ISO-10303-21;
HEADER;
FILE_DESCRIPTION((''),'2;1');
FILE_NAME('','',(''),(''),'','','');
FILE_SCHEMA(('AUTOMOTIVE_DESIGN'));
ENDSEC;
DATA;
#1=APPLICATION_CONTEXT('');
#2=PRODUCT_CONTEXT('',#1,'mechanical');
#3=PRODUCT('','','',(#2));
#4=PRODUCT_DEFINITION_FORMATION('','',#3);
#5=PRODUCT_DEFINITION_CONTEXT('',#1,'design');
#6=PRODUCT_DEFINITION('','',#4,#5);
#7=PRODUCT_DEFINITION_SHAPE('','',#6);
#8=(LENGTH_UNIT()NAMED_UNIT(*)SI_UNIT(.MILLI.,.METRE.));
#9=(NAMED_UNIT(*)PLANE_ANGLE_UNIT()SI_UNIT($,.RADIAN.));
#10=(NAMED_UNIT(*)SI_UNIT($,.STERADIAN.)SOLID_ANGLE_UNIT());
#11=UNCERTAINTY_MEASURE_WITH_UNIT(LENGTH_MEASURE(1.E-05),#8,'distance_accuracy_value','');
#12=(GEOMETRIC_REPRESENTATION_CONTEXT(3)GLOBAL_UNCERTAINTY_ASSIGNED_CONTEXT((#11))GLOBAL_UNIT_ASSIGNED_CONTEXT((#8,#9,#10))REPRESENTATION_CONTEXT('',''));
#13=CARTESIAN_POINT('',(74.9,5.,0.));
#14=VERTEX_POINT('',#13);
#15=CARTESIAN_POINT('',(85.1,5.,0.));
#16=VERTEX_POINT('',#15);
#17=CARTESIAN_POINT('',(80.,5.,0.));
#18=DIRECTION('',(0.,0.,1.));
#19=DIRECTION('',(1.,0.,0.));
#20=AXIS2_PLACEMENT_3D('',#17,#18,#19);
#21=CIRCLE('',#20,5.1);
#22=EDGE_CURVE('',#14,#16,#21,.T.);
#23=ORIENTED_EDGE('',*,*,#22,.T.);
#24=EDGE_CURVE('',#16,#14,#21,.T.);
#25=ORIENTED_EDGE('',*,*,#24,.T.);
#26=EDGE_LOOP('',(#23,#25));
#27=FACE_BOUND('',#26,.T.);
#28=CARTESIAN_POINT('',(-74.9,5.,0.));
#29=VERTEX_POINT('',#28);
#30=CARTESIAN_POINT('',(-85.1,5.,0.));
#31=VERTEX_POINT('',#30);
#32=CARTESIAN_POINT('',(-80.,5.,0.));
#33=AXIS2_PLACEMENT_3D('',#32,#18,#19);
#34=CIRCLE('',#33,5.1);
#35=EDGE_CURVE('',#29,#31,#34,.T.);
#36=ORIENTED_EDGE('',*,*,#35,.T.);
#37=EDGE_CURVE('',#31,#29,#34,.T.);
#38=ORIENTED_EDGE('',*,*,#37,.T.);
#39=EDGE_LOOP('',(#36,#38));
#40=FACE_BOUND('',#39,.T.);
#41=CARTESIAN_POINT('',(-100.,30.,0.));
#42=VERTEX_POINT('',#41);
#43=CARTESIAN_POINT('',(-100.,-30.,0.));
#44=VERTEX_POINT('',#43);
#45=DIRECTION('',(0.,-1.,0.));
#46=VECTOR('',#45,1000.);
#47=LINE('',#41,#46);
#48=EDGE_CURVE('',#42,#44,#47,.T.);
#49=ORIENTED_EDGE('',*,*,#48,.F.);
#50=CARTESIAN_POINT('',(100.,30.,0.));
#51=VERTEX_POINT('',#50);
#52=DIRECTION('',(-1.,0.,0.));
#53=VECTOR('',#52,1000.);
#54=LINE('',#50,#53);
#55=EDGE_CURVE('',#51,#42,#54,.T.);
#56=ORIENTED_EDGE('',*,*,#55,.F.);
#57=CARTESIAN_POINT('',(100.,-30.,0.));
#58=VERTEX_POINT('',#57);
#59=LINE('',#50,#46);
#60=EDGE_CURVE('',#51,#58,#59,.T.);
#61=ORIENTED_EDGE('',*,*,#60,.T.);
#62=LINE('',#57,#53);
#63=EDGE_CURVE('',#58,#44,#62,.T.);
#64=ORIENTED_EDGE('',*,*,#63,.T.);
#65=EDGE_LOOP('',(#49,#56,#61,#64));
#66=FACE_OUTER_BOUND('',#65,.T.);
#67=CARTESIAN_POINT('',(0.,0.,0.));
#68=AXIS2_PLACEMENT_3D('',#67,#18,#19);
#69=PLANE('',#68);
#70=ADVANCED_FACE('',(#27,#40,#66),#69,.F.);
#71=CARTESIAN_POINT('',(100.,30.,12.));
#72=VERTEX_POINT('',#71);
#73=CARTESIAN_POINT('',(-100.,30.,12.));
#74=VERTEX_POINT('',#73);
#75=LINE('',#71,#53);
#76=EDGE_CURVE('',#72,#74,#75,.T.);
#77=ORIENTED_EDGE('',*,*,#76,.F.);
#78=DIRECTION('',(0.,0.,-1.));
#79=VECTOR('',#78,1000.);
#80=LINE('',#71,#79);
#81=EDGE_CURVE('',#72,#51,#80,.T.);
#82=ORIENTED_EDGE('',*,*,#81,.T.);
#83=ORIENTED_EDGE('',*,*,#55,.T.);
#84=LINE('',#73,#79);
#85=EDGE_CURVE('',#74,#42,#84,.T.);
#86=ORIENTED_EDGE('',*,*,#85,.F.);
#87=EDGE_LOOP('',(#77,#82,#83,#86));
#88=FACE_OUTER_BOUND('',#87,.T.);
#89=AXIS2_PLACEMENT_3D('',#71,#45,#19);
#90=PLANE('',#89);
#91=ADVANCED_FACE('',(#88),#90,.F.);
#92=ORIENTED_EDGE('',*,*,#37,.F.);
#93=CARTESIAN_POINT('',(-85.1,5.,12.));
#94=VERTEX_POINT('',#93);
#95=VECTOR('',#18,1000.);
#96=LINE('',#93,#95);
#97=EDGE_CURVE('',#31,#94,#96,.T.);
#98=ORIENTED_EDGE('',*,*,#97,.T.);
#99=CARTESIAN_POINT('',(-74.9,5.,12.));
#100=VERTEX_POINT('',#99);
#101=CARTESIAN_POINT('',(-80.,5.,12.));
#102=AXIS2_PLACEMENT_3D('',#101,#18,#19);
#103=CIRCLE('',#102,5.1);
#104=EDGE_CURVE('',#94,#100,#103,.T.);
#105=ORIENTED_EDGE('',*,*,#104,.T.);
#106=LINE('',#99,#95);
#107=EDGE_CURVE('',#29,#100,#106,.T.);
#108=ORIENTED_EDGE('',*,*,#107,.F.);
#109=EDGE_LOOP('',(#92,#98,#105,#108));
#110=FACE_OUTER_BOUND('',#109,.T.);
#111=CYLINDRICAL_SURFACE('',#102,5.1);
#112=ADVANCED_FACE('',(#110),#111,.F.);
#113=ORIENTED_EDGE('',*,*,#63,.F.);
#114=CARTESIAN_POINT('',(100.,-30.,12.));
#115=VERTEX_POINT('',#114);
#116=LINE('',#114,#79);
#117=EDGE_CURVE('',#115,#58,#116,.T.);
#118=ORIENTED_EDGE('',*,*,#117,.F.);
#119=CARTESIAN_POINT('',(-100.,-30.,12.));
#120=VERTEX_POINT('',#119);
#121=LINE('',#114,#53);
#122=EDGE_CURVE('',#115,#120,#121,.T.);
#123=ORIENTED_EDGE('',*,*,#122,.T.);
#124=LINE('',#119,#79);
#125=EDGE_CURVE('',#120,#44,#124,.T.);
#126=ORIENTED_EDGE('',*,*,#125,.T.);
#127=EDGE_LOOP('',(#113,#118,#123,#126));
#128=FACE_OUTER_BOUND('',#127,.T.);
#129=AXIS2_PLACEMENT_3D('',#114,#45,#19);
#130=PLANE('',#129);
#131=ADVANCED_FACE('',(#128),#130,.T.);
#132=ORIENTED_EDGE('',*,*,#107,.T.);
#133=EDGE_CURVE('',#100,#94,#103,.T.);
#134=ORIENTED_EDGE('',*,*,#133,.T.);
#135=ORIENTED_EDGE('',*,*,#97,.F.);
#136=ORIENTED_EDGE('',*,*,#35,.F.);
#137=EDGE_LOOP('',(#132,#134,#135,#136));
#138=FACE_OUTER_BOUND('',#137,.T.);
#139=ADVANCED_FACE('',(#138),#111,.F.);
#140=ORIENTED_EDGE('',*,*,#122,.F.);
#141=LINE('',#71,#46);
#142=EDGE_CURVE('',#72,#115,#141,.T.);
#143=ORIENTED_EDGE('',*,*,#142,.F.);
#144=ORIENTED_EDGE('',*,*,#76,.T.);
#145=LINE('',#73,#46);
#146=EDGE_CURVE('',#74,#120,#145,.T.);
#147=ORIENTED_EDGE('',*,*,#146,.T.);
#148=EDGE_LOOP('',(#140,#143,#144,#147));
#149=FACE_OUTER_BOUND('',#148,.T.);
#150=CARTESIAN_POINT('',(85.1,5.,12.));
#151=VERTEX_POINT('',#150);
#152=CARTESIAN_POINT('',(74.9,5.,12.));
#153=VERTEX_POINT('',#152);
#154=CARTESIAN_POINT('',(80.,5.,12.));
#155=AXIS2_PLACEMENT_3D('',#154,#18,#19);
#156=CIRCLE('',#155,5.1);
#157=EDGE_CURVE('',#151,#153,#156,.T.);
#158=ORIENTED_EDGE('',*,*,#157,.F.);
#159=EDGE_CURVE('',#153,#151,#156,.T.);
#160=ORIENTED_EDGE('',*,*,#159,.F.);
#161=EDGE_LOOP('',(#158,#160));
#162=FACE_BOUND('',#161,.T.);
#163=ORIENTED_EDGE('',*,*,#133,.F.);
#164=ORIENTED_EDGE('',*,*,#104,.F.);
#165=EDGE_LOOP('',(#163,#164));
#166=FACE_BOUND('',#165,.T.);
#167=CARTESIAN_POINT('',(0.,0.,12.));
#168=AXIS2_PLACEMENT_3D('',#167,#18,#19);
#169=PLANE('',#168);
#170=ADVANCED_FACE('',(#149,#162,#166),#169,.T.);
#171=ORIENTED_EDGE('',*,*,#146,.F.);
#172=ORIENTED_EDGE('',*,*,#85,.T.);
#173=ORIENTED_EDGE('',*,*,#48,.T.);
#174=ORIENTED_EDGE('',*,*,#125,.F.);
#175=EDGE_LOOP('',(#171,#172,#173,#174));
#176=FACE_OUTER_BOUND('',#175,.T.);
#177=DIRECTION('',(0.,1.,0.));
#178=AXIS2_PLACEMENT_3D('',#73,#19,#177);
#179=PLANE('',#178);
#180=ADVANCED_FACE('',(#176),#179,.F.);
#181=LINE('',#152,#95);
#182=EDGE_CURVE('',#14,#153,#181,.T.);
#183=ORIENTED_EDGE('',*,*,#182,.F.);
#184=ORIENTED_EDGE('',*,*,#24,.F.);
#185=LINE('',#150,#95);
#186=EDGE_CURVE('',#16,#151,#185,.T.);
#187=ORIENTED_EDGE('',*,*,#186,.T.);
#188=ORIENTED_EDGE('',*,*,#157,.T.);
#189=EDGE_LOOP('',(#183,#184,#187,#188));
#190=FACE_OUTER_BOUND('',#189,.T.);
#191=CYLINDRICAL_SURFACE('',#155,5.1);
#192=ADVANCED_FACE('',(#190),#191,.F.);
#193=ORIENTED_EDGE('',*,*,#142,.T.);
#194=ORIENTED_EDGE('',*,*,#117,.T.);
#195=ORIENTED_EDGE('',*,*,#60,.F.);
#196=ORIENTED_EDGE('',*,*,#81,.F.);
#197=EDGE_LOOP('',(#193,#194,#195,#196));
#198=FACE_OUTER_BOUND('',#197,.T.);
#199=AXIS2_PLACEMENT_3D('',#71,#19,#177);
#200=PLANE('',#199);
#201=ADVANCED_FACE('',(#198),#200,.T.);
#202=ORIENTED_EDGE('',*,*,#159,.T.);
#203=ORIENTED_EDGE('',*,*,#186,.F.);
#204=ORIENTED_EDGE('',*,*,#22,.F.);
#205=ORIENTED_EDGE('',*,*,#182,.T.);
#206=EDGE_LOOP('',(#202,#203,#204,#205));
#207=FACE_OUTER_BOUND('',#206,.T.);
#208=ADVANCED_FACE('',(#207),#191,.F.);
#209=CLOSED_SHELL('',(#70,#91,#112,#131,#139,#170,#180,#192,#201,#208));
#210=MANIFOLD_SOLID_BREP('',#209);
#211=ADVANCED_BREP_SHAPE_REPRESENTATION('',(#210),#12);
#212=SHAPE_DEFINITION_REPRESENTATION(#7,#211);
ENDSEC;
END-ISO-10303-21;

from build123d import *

# Parameters (mm, degrees)
SKETCH1_W              = 200
SKETCH1_H              = 60
BOSS_EXTRUDE1_DEPTH    = 12
M12_TAPPED_HOLE1_D     = 10.2
M12_TAPPED_HOLE1_DEPTH = 29.25
M12_TAPPED_HOLE1_TIP   = 3.064389157


with BuildPart() as part:
    # Sketch1 → Boss-Extrude1 (new body)
    with BuildSketch(Plane.XY):
        Rectangle(SKETCH1_W, SKETCH1_H)
    extrude(amount=BOSS_EXTRUDE1_DEPTH)

    # M12 Tapped Hole1
    with Locations(Plane.XY.offset(12)):
        with Locations((-80, 5), (80, 5)):
            Hole(M12_TAPPED_HOLE1_D / 2, depth=M12_TAPPED_HOLE1_DEPTH)
            with Locations((0, 0, -(M12_TAPPED_HOLE1_DEPTH + M12_TAPPED_HOLE1_TIP / 2))):  # 118° drill point
                Cone(0, M12_TAPPED_HOLE1_D / 2, M12_TAPPED_HOLE1_TIP, mode=Mode.SUBTRACT)


solid = part.part
